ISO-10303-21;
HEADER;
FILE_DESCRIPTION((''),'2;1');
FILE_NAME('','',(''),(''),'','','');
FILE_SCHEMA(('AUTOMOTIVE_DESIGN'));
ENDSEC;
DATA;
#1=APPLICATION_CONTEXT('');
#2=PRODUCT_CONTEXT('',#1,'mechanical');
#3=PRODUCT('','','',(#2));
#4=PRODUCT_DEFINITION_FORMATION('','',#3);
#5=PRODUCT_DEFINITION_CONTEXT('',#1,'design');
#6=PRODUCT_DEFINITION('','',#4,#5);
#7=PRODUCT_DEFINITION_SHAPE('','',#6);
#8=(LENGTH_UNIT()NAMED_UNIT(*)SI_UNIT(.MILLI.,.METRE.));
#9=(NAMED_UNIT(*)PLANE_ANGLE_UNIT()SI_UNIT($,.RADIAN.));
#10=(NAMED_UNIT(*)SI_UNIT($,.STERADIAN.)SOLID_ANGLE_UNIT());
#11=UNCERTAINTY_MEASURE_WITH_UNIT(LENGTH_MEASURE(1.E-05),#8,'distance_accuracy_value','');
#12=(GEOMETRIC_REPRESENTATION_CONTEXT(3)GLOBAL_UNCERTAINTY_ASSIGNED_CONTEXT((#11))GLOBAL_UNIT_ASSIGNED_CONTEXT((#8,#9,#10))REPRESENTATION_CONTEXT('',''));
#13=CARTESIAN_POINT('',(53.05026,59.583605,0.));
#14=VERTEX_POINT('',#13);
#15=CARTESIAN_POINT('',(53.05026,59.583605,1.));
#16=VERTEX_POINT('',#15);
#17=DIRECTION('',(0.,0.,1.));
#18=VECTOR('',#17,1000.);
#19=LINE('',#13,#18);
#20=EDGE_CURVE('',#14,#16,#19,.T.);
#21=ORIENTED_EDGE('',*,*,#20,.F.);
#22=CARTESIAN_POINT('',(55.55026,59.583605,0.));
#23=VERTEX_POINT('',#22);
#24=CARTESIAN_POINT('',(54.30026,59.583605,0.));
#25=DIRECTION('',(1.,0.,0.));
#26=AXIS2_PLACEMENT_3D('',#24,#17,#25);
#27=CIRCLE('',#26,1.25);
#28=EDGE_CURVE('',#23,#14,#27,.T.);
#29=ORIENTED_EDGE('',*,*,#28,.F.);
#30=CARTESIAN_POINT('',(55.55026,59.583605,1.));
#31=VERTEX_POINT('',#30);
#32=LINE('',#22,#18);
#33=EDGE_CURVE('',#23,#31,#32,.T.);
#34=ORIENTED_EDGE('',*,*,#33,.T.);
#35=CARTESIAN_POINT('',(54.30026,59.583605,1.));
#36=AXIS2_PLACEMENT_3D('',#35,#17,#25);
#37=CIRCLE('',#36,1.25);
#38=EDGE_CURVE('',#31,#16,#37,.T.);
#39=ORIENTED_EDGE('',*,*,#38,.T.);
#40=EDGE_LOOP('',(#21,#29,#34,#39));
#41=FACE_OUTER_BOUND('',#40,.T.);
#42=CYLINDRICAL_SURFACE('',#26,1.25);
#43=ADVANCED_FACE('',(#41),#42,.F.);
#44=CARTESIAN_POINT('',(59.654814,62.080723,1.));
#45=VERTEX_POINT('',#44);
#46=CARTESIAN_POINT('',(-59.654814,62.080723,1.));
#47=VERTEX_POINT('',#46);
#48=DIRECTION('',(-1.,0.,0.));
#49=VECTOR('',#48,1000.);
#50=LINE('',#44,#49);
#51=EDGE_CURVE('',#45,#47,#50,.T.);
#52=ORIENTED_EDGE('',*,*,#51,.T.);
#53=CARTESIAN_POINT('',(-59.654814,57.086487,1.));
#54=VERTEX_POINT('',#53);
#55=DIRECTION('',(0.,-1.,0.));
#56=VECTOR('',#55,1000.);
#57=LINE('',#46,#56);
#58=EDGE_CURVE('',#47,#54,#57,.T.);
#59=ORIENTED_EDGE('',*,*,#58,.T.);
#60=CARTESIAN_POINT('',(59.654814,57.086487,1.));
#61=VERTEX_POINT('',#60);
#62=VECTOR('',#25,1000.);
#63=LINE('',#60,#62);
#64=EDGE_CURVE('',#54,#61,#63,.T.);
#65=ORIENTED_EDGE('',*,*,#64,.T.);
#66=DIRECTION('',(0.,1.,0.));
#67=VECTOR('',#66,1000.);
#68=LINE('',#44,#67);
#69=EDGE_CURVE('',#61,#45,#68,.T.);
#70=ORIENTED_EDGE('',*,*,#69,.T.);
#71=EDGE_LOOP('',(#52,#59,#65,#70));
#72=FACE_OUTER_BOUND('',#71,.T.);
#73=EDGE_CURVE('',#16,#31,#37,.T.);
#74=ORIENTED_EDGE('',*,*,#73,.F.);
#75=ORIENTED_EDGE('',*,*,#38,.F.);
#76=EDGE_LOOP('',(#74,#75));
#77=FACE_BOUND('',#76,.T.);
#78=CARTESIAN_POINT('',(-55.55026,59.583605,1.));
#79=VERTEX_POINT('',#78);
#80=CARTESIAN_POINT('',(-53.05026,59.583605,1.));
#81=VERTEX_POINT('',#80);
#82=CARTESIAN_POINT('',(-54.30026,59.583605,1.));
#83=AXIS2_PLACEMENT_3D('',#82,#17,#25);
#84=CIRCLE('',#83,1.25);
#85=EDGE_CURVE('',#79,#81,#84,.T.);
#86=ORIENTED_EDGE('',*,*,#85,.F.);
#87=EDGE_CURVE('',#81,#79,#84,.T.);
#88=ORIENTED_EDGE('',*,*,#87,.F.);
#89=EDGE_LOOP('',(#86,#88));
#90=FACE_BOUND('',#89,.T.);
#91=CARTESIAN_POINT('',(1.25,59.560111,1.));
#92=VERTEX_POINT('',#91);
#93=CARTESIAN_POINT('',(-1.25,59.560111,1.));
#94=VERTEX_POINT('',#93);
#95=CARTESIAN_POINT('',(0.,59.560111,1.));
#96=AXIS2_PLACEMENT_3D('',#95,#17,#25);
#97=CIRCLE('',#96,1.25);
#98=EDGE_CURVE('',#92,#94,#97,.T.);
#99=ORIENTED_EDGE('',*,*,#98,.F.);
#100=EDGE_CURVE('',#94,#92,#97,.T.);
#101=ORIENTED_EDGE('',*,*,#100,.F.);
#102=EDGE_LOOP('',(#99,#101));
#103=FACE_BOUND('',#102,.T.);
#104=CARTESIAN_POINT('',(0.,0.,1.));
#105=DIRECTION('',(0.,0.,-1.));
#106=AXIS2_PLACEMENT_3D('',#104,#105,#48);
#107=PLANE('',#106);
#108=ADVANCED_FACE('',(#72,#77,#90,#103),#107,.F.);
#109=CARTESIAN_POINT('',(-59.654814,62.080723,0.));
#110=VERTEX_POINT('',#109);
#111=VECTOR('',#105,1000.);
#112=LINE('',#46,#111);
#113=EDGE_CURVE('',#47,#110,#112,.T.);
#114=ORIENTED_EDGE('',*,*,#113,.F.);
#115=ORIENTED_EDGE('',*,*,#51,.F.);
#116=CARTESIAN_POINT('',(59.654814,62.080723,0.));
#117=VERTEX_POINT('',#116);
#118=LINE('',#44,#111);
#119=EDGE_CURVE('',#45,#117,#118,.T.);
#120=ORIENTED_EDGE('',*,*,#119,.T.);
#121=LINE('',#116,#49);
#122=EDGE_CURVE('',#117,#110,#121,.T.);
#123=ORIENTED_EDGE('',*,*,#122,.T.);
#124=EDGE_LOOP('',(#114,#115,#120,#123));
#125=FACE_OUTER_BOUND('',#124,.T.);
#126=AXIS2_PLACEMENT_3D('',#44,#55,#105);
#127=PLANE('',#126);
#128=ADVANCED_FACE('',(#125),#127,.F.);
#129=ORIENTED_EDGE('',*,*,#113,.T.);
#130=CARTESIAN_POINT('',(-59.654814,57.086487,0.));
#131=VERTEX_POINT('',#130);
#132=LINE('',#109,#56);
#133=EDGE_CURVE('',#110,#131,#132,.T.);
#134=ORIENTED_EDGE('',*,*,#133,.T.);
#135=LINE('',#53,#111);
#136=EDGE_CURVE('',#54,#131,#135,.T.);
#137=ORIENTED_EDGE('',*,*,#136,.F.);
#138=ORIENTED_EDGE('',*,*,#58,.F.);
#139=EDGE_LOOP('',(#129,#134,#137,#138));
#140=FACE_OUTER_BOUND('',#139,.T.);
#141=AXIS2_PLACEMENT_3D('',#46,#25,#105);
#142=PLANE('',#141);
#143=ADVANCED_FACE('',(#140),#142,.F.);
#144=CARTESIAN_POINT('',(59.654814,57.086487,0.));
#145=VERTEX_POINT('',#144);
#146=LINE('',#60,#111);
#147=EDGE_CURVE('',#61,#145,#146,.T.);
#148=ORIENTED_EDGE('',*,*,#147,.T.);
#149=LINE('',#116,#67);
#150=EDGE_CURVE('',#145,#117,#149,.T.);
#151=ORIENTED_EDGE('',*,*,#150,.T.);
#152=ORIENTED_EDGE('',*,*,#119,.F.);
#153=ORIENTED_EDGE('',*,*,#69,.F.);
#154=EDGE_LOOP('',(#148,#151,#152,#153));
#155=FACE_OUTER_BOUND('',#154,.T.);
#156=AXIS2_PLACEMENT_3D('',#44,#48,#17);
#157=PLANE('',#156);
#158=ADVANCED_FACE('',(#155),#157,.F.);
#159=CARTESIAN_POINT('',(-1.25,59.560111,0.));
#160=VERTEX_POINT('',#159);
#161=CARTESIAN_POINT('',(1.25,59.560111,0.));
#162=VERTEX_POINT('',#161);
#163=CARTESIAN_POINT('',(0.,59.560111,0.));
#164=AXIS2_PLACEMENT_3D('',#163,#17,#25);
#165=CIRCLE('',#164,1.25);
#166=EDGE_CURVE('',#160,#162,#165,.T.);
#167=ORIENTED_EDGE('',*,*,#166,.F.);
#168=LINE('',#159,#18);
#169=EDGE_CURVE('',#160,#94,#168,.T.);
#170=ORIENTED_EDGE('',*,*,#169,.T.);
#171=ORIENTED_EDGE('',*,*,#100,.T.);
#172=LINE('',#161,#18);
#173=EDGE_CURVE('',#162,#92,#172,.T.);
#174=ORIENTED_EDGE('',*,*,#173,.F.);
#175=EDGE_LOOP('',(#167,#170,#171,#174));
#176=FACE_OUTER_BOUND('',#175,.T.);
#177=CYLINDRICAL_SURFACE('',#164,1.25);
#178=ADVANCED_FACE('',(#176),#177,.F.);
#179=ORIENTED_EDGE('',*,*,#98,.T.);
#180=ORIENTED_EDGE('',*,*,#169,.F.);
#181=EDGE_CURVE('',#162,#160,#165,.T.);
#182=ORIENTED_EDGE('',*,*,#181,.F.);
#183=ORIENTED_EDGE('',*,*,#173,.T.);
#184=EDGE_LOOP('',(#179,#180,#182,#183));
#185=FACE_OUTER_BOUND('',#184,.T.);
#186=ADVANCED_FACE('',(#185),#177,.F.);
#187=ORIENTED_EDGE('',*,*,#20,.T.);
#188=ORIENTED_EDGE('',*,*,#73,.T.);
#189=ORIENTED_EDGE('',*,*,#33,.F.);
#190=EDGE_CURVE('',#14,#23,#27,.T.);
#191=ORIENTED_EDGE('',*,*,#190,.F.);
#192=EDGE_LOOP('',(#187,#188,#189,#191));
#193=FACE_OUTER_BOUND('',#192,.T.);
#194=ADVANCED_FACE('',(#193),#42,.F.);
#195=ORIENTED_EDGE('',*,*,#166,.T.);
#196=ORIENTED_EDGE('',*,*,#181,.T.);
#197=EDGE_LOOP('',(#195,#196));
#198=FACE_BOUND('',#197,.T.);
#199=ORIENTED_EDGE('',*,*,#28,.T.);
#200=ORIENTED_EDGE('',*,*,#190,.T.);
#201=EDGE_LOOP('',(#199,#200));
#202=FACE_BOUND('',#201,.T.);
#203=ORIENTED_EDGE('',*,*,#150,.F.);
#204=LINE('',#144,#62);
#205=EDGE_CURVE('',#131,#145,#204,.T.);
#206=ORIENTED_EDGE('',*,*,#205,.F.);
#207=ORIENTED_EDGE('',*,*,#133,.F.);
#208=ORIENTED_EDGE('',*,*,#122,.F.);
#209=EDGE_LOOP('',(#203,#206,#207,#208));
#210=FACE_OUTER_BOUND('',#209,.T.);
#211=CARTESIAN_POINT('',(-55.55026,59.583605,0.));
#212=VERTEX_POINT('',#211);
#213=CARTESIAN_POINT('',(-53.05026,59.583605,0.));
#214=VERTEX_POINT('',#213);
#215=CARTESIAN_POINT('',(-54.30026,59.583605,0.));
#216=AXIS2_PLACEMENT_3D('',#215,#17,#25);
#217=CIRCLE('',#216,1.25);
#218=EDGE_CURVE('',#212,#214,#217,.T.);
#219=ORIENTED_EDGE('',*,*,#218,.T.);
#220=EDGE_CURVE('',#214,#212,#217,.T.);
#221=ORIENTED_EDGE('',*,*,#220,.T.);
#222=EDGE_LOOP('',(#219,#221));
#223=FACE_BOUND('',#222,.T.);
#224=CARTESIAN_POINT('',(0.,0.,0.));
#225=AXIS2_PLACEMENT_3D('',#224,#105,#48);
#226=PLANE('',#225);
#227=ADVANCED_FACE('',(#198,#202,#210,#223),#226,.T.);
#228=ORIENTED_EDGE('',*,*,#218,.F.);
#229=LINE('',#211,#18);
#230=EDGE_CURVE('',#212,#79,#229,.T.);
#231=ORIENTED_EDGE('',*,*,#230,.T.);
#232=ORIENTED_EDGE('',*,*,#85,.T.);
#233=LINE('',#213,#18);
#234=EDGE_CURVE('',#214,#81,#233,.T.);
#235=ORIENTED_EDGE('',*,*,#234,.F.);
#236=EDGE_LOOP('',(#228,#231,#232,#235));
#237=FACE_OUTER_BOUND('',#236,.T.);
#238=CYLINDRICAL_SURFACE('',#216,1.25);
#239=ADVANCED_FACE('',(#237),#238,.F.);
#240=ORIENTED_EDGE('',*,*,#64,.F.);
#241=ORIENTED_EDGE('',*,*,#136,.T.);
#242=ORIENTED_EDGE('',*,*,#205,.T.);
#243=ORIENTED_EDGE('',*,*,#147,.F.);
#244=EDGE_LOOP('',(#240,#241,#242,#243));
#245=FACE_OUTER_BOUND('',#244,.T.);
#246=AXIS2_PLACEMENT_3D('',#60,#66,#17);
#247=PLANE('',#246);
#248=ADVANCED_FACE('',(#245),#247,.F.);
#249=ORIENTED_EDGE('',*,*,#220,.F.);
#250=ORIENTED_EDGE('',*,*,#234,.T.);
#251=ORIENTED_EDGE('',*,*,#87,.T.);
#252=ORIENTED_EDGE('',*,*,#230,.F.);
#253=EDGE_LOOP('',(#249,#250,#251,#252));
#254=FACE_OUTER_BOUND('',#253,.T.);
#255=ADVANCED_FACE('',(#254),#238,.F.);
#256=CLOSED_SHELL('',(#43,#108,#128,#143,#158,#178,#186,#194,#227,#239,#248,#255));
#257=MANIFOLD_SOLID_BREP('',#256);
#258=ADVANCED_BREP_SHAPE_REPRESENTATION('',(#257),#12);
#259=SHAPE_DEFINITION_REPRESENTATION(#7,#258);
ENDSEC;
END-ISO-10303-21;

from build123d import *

# Parameters (mm, degrees)
SKETCH1_W           = 119.309628318
SKETCH1_H           = 4.994236566
BOSS_EXTRUDE1_DEPTH = 1
SKETCH2_R           = 1.25
CUT_EXTRUDE1_DEPTH  = 1


with BuildPart() as part:
    # Sketch1 → Boss-Extrude1 (new body)
    with BuildSketch(Plane.XY):
        with Locations((0, 59.58360497)):
            Rectangle(SKETCH1_W, SKETCH1_H)
    extrude(amount=BOSS_EXTRUDE1_DEPTH)

    # Sketch2 → Cut-Extrude1 (cut)
    with BuildSketch(Plane.XY.offset(1)):
        with Locations((-54.300260115, 59.58360497)):
            Circle(SKETCH2_R)
        with Locations((0, 59.560111084)):
            Circle(SKETCH2_R)
        with Locations((54.300260115, 59.58360497)):
            Circle(SKETCH2_R)
    extrude(amount=-CUT_EXTRUDE1_DEPTH, mode=Mode.SUBTRACT)


solid = part.part
